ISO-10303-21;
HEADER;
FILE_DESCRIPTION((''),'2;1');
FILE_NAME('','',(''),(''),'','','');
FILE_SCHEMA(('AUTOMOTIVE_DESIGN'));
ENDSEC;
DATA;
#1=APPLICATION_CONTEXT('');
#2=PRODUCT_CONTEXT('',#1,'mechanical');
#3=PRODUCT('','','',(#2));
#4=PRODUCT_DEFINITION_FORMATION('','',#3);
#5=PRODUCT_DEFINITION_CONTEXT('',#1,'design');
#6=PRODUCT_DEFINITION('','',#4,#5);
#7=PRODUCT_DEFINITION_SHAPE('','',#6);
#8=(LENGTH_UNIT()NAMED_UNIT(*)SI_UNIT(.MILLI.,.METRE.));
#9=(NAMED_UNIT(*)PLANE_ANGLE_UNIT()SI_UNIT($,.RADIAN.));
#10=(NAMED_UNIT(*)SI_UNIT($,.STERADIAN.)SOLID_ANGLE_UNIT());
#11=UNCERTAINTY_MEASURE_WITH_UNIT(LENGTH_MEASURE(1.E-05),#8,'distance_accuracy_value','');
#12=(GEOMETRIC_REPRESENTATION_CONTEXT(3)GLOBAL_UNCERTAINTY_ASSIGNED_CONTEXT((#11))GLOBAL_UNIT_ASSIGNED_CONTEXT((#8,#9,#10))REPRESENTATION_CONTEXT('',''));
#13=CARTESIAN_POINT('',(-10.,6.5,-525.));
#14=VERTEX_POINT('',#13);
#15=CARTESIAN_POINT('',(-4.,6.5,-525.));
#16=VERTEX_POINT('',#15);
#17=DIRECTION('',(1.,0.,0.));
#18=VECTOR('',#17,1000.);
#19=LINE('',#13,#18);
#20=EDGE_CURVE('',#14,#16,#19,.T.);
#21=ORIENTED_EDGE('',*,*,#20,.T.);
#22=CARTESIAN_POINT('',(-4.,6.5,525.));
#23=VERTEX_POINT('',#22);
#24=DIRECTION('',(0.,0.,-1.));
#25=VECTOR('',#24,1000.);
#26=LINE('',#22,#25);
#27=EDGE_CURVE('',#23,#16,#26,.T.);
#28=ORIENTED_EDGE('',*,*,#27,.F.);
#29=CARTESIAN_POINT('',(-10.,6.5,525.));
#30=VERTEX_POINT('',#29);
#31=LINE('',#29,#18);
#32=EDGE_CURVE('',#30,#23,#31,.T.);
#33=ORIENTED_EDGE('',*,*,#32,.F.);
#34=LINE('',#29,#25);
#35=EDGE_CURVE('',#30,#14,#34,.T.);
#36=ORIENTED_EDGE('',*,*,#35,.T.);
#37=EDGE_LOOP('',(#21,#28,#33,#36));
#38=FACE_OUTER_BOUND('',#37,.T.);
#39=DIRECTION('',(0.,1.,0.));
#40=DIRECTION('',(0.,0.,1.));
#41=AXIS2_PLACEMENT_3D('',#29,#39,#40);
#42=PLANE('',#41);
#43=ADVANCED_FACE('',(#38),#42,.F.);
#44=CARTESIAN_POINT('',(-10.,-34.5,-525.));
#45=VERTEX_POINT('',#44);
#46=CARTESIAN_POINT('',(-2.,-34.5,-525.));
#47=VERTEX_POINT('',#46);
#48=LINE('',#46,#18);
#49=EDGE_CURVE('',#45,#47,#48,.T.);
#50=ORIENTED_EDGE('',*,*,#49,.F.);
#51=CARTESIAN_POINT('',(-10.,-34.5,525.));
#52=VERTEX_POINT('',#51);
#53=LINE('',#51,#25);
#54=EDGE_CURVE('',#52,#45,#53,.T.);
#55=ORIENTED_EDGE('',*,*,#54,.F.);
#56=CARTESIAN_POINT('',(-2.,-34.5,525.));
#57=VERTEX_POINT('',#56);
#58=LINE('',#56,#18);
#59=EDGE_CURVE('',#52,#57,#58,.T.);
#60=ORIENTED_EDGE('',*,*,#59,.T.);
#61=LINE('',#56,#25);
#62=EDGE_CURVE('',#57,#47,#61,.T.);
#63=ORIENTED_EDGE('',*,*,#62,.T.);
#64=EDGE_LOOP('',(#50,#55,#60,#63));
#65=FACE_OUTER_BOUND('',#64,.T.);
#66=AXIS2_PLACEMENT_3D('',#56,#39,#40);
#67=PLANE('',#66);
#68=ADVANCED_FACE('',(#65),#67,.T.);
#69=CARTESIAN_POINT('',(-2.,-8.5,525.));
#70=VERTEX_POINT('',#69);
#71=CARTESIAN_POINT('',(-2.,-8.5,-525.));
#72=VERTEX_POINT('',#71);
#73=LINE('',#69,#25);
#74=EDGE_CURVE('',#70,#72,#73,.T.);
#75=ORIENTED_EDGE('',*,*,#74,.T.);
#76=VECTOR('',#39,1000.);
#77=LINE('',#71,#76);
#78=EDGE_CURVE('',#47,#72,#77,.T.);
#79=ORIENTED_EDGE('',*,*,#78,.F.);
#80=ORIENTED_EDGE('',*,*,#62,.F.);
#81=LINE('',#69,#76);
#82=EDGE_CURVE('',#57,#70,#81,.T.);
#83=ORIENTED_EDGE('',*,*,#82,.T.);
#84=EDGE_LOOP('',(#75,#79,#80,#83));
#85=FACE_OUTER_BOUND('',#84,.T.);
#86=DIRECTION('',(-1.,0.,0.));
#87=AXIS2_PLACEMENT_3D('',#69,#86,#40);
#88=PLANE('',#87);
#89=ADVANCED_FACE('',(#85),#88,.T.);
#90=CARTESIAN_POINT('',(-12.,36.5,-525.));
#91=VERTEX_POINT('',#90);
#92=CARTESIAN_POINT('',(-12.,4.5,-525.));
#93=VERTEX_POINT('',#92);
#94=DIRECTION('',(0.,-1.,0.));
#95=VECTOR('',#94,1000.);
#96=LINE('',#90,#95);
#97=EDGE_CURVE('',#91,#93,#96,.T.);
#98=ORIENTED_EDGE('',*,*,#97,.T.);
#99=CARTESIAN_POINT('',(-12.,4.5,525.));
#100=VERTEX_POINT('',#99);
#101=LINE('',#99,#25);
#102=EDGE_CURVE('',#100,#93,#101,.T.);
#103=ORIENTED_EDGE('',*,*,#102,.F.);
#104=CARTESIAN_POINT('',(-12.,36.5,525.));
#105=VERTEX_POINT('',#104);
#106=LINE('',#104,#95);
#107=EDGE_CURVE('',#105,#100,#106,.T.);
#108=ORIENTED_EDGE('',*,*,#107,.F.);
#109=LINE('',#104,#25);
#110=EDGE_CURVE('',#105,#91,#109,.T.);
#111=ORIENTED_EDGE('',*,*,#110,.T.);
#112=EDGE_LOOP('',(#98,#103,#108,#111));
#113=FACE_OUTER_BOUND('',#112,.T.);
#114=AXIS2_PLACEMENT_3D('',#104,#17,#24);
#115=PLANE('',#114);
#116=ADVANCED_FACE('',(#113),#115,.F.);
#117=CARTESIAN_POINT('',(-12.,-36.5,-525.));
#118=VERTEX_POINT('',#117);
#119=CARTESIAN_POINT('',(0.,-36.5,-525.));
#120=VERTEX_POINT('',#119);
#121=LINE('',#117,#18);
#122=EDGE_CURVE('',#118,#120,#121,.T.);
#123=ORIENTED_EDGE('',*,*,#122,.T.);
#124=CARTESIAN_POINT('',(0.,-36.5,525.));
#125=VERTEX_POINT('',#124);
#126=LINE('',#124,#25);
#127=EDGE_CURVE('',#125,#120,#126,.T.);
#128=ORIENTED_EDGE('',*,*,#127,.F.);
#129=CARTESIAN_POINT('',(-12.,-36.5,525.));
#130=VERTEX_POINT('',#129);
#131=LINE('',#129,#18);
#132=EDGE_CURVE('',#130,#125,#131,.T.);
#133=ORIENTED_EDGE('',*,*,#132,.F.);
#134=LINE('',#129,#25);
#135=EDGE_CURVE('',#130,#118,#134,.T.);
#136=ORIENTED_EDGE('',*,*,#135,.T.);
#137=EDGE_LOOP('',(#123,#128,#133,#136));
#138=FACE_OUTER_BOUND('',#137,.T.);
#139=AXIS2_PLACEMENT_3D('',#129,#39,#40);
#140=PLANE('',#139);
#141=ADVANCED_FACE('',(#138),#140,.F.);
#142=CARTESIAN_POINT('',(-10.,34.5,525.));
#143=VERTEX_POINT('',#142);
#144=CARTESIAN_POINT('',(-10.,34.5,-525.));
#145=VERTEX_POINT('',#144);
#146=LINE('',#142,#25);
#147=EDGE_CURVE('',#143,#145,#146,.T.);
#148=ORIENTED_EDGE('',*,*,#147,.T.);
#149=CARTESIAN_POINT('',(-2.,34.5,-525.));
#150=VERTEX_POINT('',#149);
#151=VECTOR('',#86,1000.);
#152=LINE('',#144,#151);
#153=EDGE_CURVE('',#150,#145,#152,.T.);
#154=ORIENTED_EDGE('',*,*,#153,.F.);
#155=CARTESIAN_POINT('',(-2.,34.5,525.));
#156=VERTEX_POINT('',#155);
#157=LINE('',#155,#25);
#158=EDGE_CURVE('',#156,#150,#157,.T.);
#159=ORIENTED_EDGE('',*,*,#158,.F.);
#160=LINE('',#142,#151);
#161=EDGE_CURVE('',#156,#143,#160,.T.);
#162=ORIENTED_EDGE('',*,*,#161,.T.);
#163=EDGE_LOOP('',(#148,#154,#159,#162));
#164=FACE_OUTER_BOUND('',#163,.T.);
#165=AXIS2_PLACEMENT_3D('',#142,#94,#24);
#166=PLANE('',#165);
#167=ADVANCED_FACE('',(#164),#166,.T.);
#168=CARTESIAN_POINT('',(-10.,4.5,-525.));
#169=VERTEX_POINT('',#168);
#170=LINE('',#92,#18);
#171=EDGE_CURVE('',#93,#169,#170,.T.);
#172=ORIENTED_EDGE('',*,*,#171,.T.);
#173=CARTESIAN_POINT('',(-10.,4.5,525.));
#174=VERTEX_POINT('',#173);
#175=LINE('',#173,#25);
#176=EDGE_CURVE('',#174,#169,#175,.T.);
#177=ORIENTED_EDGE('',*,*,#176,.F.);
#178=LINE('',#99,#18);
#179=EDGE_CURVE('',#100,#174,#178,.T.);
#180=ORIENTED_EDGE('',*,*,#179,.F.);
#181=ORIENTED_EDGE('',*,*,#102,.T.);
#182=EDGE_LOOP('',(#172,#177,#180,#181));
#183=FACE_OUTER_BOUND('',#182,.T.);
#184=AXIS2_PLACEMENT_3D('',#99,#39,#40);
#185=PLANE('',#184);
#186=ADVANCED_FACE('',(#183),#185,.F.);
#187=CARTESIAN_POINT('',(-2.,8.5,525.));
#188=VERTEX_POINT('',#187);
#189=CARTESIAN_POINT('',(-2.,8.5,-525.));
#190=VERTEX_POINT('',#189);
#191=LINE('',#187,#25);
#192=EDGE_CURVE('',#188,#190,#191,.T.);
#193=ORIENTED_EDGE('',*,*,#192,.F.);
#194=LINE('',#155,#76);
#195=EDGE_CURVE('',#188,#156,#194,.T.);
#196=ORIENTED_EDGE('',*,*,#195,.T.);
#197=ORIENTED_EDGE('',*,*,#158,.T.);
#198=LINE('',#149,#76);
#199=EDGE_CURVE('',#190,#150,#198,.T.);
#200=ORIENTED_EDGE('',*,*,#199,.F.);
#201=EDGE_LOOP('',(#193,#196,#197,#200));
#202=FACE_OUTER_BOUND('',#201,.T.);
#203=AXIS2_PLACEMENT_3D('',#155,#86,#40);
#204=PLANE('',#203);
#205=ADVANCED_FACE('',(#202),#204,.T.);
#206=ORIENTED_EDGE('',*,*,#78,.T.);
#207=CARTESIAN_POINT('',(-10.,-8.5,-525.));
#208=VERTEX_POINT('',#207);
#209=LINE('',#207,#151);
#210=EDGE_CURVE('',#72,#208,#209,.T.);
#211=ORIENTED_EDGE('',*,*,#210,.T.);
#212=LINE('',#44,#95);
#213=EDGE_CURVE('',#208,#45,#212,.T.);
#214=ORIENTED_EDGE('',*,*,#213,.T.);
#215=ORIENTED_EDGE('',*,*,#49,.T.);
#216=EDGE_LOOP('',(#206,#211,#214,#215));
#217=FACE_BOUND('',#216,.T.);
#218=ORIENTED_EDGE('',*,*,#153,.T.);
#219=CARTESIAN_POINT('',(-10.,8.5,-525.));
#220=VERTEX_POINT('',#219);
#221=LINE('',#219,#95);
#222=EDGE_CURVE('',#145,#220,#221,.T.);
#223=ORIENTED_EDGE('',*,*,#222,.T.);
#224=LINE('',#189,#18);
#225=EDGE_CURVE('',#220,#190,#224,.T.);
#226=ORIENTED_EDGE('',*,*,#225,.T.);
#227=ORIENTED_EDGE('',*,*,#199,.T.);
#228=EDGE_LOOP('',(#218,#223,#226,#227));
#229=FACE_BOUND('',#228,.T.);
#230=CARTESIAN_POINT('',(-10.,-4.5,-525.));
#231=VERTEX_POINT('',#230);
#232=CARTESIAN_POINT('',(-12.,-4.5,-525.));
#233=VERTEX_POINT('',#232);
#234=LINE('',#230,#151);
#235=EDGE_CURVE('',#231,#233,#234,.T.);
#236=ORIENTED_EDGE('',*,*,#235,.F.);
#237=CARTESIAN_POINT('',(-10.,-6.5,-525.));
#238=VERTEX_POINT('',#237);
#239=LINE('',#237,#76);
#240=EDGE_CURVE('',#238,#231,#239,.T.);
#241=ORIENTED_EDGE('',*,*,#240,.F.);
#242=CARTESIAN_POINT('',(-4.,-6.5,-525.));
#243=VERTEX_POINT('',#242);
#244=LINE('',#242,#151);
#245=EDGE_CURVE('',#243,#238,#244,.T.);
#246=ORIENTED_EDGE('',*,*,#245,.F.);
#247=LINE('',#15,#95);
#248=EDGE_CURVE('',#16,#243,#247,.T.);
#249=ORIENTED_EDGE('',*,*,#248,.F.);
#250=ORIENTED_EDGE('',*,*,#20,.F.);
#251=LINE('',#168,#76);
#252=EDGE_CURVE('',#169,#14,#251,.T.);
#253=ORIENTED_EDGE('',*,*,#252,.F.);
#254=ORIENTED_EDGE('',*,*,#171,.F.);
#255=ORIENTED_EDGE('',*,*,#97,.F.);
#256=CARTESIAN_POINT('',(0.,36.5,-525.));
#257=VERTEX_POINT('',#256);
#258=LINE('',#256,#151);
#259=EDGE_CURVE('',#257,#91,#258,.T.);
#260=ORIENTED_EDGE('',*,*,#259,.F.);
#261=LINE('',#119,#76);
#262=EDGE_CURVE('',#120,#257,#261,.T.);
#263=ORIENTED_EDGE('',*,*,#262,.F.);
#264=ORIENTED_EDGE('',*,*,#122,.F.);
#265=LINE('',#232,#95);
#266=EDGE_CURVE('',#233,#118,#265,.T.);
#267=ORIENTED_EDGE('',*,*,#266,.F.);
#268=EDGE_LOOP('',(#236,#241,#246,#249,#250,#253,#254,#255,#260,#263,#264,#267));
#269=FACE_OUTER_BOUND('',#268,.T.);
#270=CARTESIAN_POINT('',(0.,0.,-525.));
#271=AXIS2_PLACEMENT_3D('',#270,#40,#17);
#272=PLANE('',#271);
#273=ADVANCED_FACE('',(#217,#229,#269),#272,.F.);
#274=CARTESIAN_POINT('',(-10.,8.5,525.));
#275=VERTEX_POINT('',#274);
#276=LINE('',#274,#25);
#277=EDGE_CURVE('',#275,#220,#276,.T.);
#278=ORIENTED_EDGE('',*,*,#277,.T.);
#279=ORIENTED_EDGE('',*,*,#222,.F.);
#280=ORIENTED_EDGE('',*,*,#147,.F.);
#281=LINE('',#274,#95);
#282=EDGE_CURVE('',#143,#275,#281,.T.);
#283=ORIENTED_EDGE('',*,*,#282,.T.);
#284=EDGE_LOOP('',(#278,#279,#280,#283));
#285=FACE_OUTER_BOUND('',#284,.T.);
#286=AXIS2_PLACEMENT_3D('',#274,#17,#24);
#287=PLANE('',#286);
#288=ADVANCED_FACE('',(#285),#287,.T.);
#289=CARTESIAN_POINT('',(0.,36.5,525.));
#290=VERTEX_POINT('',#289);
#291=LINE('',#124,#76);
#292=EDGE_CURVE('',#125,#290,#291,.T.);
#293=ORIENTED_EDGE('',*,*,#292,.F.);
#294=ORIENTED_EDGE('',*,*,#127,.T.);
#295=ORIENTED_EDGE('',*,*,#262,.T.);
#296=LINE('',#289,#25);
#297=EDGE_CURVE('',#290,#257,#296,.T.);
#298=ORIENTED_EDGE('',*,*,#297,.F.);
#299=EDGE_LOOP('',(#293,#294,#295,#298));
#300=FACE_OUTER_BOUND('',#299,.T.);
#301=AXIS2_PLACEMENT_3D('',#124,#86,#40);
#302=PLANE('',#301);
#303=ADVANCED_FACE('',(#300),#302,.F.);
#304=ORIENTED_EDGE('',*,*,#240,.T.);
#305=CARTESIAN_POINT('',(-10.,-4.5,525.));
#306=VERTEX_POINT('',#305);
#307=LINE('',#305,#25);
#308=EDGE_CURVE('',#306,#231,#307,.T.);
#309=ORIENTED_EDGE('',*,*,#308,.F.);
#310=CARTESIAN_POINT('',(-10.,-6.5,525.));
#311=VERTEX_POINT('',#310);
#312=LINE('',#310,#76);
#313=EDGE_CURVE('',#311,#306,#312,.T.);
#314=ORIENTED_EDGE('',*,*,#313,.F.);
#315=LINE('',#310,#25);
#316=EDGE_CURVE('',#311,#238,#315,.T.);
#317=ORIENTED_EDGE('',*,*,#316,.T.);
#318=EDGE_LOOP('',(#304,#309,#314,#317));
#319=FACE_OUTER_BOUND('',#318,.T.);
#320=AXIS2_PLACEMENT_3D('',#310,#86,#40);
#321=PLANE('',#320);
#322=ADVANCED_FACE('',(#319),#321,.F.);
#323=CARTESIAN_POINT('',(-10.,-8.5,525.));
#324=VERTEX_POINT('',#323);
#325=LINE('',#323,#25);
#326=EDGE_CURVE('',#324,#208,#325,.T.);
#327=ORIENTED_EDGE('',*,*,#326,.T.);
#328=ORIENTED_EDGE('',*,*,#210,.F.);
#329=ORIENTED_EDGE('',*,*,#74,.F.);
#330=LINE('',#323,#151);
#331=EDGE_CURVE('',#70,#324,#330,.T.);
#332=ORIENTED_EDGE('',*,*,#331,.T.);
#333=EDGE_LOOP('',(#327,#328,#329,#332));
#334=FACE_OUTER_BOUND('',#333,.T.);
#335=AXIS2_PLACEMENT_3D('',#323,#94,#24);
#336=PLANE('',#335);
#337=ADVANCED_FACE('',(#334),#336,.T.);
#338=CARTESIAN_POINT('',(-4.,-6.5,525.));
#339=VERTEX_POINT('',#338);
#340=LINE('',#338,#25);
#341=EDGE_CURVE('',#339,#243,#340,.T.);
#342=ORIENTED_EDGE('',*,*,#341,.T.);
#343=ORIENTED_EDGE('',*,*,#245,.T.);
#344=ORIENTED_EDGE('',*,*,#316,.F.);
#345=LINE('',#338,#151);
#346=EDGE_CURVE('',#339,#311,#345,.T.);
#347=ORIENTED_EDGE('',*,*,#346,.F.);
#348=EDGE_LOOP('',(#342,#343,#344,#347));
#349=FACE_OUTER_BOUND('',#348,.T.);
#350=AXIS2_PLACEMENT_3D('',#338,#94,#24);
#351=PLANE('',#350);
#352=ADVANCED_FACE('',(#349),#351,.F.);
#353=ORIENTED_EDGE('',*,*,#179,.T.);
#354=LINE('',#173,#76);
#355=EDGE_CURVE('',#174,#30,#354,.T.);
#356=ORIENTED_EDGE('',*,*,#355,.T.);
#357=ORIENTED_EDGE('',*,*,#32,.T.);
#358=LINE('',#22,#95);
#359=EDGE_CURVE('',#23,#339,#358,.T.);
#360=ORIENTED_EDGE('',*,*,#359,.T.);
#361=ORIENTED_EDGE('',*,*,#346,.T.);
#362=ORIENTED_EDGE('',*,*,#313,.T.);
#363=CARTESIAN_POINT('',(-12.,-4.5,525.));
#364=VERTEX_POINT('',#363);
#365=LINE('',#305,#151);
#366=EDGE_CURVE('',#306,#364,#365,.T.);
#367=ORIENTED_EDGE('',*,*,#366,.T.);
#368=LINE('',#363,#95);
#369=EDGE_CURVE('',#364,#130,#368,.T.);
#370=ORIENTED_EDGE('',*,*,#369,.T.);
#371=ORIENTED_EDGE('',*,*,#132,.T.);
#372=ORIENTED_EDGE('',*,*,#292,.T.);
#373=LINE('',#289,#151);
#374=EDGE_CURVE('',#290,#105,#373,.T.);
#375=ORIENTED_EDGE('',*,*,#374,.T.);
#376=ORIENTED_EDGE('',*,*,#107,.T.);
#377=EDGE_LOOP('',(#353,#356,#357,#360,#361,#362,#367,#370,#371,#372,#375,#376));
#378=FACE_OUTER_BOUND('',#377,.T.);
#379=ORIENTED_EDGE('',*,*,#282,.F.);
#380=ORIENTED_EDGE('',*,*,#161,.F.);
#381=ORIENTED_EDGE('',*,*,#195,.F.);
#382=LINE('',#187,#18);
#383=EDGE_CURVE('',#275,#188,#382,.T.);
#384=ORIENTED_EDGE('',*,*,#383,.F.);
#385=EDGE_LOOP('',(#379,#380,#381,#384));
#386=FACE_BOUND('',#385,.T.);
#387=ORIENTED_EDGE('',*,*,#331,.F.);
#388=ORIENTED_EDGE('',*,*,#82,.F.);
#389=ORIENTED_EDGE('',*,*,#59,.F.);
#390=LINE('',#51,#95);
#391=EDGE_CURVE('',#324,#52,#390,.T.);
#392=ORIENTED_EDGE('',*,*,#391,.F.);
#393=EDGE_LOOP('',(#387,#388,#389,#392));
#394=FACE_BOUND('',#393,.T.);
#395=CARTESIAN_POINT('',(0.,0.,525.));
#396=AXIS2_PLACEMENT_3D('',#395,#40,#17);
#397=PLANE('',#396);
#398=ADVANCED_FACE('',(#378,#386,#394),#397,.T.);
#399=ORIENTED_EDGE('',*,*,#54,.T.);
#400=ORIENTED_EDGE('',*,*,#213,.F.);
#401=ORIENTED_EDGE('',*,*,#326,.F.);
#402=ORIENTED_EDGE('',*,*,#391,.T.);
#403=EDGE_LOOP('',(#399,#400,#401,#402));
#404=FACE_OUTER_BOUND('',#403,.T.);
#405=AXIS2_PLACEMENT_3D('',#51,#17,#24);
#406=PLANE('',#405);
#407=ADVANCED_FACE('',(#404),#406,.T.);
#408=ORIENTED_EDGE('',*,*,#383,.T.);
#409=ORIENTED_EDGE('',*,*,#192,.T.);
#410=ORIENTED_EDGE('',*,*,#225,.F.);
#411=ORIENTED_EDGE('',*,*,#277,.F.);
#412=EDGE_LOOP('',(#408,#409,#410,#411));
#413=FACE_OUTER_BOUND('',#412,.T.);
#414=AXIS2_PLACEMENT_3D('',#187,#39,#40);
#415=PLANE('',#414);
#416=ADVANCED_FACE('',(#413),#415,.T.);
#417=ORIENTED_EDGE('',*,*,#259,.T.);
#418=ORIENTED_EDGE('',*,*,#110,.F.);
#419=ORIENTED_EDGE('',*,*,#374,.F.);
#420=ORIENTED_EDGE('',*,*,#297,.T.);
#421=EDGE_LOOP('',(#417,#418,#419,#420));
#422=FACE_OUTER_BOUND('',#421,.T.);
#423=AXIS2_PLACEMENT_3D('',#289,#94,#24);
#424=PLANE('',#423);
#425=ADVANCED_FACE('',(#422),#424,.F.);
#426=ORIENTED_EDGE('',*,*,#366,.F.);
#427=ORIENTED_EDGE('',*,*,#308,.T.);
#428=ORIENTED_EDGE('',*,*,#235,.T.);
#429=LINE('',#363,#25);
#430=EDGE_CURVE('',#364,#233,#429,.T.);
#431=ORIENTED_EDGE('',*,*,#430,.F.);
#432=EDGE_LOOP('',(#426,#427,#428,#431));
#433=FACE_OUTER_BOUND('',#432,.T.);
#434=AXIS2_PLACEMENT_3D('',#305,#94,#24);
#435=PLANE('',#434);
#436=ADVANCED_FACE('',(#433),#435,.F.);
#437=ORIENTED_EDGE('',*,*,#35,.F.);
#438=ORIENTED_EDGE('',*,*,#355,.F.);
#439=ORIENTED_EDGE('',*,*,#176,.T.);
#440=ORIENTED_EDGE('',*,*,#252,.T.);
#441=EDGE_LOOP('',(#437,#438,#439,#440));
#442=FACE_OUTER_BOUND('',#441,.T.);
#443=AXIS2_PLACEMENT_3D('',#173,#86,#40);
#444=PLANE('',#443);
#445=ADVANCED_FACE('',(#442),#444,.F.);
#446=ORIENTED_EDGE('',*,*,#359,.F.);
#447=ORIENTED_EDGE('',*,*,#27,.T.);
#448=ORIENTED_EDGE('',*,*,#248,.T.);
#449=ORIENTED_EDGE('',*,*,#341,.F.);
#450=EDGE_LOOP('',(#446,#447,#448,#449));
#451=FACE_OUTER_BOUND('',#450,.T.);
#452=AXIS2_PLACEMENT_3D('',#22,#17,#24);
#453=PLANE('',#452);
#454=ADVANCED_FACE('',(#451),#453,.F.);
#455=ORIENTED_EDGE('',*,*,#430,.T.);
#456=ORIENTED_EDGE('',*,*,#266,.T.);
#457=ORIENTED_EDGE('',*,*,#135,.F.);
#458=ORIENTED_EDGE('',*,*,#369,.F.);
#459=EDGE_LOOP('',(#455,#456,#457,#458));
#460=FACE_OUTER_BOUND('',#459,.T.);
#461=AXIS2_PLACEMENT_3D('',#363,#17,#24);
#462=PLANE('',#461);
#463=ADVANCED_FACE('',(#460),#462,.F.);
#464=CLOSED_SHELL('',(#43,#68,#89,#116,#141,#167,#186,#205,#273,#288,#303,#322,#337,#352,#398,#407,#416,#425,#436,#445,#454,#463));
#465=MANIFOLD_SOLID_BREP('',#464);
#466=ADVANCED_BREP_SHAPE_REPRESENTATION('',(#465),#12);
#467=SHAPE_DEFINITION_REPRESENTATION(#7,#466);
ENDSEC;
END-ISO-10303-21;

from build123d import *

# Parameters (mm, degrees)
SKETCH_1_W      = 8
SKETCH_1_H      = 26
EXTRUDE_1_DEPTH = 525


with BuildPart() as part:
    # 草图1 → 凸台-拉伸1 (new, symmetric)
    with BuildSketch(Plane.XY):
        Polygon((-12, 4.5), (-10, 4.5), (-10, 6.5), (-4, 6.5), (-4, -6.5), (-10, -6.5), (-10, -4.5), (-12, -4.5), (-12, -36.5), (0, -36.5), (0, 36.5), (-12, 36.5), align=None)
        with Locations((-6, -21.5)):
            Rectangle(SKETCH_1_W, SKETCH_1_H, mode=Mode.SUBTRACT)
        with Locations((-6, 21.5)):
            Rectangle(SKETCH_1_W, SKETCH_1_H, mode=Mode.SUBTRACT)
    extrude(amount=EXTRUDE_1_DEPTH, both=True)


solid = part.part
